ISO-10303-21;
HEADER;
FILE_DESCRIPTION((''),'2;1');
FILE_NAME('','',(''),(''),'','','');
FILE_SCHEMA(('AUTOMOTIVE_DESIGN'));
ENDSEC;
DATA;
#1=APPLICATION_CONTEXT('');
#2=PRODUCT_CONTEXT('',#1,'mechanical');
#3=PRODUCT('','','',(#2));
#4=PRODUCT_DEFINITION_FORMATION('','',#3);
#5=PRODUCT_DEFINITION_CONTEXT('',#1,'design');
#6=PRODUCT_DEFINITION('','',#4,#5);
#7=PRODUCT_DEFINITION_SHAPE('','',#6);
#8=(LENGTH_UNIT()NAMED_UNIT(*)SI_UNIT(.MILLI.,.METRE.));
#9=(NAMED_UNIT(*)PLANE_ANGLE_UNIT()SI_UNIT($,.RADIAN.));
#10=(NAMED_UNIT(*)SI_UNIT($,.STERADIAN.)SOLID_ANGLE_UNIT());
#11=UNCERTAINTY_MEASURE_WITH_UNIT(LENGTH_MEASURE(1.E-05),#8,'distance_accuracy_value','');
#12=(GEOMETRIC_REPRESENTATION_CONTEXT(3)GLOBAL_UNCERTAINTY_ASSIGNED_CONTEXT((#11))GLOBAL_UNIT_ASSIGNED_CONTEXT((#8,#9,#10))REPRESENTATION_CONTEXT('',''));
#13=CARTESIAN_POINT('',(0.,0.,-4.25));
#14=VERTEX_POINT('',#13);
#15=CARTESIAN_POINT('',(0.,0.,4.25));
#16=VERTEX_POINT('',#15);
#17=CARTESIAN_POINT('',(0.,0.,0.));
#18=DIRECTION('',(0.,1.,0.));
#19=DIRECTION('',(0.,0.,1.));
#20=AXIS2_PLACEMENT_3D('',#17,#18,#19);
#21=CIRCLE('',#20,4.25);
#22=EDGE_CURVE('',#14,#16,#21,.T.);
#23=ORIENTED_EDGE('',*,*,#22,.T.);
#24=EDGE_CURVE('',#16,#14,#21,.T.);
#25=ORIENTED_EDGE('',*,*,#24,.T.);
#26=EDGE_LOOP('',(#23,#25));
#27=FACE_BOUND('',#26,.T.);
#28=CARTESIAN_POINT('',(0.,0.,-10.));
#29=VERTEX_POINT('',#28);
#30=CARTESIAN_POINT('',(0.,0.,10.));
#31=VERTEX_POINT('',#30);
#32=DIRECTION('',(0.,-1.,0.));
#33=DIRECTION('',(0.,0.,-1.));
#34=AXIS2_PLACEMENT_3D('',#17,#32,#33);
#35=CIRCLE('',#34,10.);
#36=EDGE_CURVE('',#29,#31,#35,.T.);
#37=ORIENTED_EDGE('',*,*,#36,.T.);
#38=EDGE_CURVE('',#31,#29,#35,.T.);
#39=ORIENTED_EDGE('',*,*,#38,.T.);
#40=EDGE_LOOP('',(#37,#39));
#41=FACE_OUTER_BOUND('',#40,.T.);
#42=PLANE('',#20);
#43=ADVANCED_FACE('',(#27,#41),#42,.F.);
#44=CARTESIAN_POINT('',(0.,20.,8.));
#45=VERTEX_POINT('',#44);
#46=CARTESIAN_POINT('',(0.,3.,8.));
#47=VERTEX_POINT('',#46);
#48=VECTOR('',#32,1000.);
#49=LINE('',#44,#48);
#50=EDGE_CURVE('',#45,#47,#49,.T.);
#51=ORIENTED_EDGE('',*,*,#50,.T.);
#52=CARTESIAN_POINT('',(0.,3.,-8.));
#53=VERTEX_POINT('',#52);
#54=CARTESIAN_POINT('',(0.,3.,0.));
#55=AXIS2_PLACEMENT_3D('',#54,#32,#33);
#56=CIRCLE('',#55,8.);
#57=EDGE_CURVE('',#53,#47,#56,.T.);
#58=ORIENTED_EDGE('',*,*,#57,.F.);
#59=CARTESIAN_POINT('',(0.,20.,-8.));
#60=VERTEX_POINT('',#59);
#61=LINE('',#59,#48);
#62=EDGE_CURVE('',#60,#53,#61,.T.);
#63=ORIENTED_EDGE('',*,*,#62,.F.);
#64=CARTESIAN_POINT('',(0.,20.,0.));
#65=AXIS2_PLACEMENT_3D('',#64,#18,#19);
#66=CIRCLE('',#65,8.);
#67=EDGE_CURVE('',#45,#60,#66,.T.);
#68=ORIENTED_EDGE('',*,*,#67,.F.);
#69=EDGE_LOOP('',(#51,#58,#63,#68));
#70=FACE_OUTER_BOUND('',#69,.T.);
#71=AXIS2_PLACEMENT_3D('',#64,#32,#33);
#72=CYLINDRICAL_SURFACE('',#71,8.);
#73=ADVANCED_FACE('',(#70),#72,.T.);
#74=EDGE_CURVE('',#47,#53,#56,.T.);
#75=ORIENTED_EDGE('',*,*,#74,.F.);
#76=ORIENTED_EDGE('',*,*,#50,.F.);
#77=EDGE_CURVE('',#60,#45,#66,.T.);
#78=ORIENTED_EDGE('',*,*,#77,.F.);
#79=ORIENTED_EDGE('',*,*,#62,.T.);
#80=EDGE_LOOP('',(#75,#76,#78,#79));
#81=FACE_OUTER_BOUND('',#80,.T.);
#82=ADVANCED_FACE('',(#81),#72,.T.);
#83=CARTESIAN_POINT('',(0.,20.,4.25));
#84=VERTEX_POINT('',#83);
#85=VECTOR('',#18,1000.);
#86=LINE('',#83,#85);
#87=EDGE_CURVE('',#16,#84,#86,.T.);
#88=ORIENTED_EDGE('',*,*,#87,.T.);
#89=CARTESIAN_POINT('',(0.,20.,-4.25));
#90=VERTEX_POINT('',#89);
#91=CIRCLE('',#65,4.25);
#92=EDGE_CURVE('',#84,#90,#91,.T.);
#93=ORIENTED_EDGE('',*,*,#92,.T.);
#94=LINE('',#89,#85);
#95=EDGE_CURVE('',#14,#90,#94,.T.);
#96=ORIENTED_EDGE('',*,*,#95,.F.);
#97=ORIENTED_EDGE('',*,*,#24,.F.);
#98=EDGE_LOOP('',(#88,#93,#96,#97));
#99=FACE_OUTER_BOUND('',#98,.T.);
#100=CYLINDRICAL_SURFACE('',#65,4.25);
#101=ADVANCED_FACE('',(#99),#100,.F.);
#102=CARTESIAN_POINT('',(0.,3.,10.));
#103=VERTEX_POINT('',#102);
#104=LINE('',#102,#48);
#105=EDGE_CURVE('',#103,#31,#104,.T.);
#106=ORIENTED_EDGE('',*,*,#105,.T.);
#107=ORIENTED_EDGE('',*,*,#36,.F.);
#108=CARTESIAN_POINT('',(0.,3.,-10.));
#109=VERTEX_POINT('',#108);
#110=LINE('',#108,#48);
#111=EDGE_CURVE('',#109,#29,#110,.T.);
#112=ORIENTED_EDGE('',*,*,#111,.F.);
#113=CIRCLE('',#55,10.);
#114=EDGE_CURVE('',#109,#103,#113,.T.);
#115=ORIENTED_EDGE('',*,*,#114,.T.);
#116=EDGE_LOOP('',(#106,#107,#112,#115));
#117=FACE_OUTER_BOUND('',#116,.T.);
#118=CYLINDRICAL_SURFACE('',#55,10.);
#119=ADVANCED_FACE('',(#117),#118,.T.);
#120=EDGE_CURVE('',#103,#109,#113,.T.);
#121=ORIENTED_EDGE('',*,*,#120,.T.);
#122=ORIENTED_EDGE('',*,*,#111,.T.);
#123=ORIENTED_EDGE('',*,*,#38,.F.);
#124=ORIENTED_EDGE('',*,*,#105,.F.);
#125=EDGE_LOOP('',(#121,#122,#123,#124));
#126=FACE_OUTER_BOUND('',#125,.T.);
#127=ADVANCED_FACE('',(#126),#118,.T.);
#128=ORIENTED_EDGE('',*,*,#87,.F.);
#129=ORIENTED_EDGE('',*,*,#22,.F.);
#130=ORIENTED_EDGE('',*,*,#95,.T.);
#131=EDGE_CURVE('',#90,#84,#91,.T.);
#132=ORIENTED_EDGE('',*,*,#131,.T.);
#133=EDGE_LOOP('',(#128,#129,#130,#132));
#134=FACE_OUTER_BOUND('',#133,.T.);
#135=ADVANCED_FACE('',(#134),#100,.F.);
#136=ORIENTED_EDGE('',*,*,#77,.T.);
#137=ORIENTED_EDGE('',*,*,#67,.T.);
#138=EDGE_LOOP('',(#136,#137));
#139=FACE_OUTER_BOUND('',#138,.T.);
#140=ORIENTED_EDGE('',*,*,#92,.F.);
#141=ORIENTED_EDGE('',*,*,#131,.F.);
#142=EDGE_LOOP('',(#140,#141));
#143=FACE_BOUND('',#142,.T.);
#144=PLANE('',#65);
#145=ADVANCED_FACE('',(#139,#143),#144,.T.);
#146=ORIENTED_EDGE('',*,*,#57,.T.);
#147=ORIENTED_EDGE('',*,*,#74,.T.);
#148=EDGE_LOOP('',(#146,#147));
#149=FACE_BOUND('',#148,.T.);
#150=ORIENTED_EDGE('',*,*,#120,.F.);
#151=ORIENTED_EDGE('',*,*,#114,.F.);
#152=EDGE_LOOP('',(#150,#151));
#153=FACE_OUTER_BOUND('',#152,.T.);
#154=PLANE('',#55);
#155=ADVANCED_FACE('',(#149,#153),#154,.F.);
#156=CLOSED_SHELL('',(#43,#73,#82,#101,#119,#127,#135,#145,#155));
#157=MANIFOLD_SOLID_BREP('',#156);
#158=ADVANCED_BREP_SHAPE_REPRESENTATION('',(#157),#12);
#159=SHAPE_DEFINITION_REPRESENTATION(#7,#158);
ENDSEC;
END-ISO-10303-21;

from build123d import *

# Parameters (mm, degrees)
SKETCH1_R              = 8
BOSS_EXTRUDE1_DEPTH    = 20
M10_TAPPED_HOLE1_D     = 8.5
M10_TAPPED_HOLE1_DEPTH = 24.5
M10_TAPPED_HOLE1_TIP   = 2.553657631
SKETCH4_R              = 10
SKETCH4_R_2            = 8
BOSS_EXTRUDE3_DEPTH    = 3


with BuildPart() as part:
    # Sketch1 → Boss-Extrude1 (new body)
    with BuildSketch(Plane(origin=(0, 0, 0), x_dir=(1, 0, 0), z_dir=(0, 1, 0))):
        with Locations(Location((0, 0, 0), (0, 0, 270))):
            Circle(SKETCH1_R)
    extrude(amount=BOSS_EXTRUDE1_DEPTH)

    # M10 Tapped Hole1
    with Locations(Plane(origin=(0, 20, 0), x_dir=(1, 0, 0), z_dir=(0, 1, 0))):
        with Locations((0, 0)):
            Hole(M10_TAPPED_HOLE1_D / 2, depth=M10_TAPPED_HOLE1_DEPTH)
            with Locations((0, 0, -(M10_TAPPED_HOLE1_DEPTH + M10_TAPPED_HOLE1_TIP / 2))):  # 118° drill point
                Cone(0, M10_TAPPED_HOLE1_D / 2, M10_TAPPED_HOLE1_TIP, mode=Mode.SUBTRACT)

    # Sketch4 → Boss-Extrude3 (add)
    with BuildSketch(Plane.XZ):
        with Locations(Location((0, 0, 0), (0, 0, 270))):
            Circle(SKETCH4_R)
        with Locations(Location((0, 0, 0), (0, 0, 270))):
            Circle(SKETCH4_R_2, mode=Mode.SUBTRACT)
    extrude(amount=-BOSS_EXTRUDE3_DEPTH)


solid = part.part
